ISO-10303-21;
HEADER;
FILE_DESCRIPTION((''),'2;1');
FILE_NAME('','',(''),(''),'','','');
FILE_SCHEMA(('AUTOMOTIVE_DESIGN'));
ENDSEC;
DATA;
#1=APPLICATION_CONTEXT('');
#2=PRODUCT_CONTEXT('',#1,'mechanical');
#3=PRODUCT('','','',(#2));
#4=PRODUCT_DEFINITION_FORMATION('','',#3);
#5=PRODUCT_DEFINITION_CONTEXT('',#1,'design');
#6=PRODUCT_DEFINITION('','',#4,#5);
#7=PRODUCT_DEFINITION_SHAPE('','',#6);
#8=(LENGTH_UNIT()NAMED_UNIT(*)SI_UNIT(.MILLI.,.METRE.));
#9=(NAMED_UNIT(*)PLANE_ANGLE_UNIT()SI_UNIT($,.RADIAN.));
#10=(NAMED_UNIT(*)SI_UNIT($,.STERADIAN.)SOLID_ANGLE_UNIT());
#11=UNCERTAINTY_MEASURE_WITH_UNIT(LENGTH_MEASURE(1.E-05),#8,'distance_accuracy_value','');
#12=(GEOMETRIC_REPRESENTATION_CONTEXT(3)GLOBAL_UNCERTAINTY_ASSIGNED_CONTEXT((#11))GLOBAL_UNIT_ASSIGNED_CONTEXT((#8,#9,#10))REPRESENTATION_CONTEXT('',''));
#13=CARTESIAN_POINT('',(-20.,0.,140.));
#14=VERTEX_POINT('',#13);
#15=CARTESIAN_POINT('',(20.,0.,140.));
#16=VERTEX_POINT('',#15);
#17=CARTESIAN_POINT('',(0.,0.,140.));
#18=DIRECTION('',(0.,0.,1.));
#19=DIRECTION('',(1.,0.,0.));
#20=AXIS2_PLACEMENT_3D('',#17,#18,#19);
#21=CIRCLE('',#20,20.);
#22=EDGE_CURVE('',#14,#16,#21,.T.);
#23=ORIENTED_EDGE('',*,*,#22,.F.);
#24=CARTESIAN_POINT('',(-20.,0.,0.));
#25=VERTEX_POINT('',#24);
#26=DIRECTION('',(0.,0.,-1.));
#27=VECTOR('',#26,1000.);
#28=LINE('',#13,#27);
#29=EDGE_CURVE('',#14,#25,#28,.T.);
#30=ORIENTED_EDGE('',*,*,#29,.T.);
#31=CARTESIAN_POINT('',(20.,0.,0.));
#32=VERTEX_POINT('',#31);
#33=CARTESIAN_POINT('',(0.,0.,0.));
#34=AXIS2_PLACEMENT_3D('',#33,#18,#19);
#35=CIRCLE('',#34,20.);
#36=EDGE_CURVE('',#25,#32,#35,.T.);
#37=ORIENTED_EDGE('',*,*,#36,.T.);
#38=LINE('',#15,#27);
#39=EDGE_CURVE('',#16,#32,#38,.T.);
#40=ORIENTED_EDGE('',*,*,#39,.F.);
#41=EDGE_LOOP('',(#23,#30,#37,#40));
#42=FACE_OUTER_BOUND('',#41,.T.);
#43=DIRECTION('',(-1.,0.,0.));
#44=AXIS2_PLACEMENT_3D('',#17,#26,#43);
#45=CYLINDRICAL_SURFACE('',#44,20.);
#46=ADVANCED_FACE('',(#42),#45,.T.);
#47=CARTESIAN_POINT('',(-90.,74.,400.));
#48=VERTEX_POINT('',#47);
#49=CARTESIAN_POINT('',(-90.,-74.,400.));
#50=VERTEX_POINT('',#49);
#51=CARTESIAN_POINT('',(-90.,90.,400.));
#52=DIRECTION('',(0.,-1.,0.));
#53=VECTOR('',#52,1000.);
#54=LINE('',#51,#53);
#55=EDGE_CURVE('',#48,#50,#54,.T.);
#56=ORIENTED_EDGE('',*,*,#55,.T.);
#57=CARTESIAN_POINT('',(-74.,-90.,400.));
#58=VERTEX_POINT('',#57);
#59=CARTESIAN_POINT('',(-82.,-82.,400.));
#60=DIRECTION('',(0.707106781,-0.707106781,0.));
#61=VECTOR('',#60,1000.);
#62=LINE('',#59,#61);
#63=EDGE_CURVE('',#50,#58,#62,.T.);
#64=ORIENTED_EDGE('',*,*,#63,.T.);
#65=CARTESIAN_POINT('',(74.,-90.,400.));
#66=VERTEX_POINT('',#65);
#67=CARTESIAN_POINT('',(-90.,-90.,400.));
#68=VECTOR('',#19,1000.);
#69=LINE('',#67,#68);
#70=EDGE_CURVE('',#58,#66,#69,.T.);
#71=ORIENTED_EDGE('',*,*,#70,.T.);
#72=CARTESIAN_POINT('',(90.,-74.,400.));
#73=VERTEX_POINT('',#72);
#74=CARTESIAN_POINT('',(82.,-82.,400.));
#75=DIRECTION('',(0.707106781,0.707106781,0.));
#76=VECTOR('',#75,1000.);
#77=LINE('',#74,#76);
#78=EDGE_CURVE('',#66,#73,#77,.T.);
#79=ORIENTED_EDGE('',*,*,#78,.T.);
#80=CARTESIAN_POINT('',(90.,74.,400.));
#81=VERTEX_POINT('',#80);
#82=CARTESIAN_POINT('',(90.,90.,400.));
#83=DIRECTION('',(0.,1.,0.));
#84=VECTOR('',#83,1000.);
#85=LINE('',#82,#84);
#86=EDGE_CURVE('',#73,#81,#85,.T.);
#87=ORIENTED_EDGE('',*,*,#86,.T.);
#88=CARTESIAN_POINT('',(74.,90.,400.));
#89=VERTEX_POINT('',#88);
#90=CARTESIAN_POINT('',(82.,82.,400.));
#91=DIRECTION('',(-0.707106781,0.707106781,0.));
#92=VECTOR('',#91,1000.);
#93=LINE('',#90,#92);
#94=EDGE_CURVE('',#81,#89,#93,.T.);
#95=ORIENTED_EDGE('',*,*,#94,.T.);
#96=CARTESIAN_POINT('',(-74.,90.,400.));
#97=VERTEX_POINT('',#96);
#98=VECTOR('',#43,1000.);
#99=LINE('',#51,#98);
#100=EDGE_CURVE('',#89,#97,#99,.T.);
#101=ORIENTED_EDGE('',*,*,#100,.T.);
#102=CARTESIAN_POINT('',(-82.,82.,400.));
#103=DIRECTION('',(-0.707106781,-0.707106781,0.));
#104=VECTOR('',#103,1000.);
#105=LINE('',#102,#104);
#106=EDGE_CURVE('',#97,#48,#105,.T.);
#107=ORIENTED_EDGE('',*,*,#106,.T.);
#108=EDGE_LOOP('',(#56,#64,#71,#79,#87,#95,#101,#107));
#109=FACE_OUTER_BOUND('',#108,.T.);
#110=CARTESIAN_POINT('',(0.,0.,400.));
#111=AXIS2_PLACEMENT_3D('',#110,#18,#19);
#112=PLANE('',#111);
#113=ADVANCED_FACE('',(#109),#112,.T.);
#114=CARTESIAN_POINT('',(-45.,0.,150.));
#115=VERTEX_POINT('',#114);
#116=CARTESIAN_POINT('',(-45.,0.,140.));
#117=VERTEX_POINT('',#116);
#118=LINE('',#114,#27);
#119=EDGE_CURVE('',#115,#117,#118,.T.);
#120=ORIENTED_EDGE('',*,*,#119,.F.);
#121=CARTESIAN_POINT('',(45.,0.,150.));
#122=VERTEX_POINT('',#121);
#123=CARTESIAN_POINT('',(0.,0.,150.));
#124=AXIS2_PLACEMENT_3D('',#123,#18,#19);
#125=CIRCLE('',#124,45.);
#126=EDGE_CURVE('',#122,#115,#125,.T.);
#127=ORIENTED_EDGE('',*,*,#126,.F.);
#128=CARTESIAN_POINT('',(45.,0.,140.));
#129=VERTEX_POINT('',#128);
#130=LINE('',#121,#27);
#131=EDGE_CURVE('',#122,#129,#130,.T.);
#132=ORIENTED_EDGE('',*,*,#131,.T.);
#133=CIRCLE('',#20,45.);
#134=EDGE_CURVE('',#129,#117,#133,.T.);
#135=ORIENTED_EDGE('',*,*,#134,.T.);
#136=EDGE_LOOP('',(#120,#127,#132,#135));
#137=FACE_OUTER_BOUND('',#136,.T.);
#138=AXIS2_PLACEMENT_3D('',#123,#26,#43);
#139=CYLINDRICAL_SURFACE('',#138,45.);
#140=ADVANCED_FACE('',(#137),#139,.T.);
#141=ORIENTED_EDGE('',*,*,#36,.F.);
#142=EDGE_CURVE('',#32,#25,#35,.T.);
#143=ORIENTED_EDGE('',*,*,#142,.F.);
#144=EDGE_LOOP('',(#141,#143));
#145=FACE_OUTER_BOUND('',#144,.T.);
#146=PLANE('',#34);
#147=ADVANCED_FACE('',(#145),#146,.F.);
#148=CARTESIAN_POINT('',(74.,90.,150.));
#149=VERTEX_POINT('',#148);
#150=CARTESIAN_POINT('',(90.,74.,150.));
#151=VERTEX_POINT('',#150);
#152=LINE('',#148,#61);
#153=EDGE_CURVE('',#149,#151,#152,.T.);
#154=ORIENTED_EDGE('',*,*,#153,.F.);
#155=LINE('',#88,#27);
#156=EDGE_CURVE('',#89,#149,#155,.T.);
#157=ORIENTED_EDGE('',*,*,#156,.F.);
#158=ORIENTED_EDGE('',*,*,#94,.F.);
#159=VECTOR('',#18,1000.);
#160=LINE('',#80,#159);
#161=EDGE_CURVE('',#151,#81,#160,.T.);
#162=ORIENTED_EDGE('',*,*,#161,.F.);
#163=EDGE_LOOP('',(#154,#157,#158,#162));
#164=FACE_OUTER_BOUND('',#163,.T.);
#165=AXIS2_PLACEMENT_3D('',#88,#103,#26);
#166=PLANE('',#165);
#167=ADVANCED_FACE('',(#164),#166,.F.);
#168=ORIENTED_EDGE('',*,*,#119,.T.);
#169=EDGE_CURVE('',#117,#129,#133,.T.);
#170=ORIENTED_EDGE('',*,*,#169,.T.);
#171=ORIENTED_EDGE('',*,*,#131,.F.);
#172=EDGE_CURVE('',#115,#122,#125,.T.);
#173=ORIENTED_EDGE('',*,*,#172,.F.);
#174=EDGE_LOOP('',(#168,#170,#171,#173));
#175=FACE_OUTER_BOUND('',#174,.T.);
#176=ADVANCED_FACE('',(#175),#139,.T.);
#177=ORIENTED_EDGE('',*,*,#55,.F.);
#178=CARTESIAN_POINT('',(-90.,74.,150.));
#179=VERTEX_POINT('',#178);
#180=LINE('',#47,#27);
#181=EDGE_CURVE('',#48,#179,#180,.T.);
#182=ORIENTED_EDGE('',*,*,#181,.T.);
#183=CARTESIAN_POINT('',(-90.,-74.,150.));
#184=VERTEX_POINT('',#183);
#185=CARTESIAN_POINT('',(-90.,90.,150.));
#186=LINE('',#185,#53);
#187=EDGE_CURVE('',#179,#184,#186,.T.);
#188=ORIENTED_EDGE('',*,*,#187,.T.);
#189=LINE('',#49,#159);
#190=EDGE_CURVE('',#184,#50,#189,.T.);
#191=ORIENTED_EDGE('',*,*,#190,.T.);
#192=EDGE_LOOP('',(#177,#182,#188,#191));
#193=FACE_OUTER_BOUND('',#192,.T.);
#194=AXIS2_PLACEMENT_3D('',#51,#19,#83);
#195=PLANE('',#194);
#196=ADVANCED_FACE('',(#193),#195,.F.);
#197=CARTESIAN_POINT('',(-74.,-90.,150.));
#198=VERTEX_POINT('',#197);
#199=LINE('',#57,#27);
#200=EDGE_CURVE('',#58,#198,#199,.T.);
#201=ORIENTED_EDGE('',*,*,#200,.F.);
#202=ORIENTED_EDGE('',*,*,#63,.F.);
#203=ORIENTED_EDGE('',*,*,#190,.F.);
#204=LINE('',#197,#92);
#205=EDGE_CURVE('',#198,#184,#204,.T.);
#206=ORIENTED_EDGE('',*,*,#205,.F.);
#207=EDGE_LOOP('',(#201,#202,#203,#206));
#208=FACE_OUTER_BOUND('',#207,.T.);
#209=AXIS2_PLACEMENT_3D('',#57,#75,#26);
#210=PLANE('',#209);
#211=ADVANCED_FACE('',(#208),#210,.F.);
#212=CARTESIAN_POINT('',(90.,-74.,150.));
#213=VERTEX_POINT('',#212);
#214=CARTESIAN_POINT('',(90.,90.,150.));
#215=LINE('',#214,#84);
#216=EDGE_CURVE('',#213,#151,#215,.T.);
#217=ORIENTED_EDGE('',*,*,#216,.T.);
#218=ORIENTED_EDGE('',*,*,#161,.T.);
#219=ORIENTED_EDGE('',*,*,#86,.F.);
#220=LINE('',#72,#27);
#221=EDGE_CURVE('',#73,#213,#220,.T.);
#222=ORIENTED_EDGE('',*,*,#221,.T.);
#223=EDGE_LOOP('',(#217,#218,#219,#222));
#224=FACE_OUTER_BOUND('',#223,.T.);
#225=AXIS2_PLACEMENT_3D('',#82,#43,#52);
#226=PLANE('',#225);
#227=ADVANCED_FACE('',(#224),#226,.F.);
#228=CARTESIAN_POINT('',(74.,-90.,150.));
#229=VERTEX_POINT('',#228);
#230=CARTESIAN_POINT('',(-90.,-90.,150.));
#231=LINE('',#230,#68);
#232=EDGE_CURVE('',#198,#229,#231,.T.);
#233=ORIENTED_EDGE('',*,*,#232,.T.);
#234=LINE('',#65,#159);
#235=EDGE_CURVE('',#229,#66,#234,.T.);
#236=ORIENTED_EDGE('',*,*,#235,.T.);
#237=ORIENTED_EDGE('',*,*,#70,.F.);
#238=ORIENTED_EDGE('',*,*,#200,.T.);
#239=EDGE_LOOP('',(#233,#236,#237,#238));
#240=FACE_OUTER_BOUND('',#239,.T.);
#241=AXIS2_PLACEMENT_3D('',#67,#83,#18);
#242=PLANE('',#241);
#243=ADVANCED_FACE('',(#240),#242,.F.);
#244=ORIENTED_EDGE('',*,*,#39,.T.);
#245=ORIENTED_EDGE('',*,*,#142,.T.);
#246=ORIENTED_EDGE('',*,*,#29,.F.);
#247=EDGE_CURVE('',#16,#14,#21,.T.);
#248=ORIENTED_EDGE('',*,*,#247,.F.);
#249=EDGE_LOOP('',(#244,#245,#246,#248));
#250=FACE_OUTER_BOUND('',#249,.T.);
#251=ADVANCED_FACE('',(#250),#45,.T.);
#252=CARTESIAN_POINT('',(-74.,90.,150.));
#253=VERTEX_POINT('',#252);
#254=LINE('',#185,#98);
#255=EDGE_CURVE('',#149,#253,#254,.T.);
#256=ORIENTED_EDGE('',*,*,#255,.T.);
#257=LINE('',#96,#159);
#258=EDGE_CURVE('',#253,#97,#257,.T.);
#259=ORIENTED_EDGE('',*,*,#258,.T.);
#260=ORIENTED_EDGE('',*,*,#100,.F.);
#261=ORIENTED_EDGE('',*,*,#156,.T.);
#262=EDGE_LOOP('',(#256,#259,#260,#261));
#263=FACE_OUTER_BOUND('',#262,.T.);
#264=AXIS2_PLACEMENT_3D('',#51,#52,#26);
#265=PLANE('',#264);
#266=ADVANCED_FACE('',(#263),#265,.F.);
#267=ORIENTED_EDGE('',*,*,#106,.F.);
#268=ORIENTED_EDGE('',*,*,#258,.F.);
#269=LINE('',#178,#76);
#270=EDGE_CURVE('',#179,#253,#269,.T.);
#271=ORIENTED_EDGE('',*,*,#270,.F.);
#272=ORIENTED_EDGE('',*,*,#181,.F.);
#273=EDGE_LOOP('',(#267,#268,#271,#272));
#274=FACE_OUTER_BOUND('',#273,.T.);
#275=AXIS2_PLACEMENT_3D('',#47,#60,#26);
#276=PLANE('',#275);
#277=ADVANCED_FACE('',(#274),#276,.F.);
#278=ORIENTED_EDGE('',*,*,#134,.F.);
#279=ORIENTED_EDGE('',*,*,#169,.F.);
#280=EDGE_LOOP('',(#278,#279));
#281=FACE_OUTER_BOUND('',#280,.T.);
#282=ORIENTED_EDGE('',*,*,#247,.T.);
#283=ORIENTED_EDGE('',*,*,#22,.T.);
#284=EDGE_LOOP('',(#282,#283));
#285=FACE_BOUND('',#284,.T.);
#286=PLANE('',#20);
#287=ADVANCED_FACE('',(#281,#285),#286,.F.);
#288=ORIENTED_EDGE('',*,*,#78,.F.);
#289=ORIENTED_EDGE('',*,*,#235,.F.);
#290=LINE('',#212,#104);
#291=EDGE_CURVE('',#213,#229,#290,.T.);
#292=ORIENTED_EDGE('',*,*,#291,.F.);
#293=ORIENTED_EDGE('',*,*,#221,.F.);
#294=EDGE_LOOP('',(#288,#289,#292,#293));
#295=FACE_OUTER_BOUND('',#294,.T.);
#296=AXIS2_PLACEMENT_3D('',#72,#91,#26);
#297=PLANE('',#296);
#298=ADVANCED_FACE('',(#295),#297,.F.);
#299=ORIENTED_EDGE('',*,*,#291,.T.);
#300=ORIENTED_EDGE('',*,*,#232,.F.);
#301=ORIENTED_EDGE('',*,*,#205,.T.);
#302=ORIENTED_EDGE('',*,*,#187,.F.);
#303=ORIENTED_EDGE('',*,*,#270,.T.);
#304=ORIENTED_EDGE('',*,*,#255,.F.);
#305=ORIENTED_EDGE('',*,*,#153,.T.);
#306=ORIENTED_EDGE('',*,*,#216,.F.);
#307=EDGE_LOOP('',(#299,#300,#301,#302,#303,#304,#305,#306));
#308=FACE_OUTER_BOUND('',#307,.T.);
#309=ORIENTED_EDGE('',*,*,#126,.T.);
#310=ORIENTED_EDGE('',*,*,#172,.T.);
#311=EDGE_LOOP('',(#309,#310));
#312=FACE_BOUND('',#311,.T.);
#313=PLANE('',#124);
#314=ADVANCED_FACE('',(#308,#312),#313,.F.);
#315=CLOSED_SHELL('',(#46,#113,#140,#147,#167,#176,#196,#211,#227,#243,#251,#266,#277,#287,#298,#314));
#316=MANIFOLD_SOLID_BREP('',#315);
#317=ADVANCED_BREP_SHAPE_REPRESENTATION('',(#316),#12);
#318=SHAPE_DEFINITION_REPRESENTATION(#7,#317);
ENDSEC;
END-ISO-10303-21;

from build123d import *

# Parameters (mm, degrees)
SKETCH1_R           = 20
BOSS_EXTRUDE1_DEPTH = 140
SKETCH2_R           = 45
BOSS_EXTRUDE2_DEPTH = 10
SKETCH3_W           = 180
SKETCH3_H           = 180
BOSS_EXTRUDE3_DEPTH = 250
CHAMFER1_SIZE       = 16


with BuildPart() as part:
    # Sketch1 → Boss-Extrude1 (new body)
    with BuildSketch(Plane.XY):
        Circle(SKETCH1_R)
    extrude(amount=BOSS_EXTRUDE1_DEPTH)

    # Sketch2 → Boss-Extrude2 (add)
    with BuildSketch(Plane.XY.offset(140)):
        Circle(SKETCH2_R)
    extrude(amount=BOSS_EXTRUDE2_DEPTH)

    # Sketch3 → Boss-Extrude3 (add)
    with BuildSketch(Plane.XY.offset(150)):
        Rectangle(SKETCH3_W, SKETCH3_H)
    extrude(amount=BOSS_EXTRUDE3_DEPTH)

    # Chamfer1
    chamfer1_edges = [part.edges().sort_by_distance(p)[0] for p in [
        (90, -90, 275),
        (90, 90, 275),
        (-90, 90, 275),
        (-90, -90, 275),
    ]]
    chamfer(chamfer1_edges, length=CHAMFER1_SIZE)


solid = part.part
